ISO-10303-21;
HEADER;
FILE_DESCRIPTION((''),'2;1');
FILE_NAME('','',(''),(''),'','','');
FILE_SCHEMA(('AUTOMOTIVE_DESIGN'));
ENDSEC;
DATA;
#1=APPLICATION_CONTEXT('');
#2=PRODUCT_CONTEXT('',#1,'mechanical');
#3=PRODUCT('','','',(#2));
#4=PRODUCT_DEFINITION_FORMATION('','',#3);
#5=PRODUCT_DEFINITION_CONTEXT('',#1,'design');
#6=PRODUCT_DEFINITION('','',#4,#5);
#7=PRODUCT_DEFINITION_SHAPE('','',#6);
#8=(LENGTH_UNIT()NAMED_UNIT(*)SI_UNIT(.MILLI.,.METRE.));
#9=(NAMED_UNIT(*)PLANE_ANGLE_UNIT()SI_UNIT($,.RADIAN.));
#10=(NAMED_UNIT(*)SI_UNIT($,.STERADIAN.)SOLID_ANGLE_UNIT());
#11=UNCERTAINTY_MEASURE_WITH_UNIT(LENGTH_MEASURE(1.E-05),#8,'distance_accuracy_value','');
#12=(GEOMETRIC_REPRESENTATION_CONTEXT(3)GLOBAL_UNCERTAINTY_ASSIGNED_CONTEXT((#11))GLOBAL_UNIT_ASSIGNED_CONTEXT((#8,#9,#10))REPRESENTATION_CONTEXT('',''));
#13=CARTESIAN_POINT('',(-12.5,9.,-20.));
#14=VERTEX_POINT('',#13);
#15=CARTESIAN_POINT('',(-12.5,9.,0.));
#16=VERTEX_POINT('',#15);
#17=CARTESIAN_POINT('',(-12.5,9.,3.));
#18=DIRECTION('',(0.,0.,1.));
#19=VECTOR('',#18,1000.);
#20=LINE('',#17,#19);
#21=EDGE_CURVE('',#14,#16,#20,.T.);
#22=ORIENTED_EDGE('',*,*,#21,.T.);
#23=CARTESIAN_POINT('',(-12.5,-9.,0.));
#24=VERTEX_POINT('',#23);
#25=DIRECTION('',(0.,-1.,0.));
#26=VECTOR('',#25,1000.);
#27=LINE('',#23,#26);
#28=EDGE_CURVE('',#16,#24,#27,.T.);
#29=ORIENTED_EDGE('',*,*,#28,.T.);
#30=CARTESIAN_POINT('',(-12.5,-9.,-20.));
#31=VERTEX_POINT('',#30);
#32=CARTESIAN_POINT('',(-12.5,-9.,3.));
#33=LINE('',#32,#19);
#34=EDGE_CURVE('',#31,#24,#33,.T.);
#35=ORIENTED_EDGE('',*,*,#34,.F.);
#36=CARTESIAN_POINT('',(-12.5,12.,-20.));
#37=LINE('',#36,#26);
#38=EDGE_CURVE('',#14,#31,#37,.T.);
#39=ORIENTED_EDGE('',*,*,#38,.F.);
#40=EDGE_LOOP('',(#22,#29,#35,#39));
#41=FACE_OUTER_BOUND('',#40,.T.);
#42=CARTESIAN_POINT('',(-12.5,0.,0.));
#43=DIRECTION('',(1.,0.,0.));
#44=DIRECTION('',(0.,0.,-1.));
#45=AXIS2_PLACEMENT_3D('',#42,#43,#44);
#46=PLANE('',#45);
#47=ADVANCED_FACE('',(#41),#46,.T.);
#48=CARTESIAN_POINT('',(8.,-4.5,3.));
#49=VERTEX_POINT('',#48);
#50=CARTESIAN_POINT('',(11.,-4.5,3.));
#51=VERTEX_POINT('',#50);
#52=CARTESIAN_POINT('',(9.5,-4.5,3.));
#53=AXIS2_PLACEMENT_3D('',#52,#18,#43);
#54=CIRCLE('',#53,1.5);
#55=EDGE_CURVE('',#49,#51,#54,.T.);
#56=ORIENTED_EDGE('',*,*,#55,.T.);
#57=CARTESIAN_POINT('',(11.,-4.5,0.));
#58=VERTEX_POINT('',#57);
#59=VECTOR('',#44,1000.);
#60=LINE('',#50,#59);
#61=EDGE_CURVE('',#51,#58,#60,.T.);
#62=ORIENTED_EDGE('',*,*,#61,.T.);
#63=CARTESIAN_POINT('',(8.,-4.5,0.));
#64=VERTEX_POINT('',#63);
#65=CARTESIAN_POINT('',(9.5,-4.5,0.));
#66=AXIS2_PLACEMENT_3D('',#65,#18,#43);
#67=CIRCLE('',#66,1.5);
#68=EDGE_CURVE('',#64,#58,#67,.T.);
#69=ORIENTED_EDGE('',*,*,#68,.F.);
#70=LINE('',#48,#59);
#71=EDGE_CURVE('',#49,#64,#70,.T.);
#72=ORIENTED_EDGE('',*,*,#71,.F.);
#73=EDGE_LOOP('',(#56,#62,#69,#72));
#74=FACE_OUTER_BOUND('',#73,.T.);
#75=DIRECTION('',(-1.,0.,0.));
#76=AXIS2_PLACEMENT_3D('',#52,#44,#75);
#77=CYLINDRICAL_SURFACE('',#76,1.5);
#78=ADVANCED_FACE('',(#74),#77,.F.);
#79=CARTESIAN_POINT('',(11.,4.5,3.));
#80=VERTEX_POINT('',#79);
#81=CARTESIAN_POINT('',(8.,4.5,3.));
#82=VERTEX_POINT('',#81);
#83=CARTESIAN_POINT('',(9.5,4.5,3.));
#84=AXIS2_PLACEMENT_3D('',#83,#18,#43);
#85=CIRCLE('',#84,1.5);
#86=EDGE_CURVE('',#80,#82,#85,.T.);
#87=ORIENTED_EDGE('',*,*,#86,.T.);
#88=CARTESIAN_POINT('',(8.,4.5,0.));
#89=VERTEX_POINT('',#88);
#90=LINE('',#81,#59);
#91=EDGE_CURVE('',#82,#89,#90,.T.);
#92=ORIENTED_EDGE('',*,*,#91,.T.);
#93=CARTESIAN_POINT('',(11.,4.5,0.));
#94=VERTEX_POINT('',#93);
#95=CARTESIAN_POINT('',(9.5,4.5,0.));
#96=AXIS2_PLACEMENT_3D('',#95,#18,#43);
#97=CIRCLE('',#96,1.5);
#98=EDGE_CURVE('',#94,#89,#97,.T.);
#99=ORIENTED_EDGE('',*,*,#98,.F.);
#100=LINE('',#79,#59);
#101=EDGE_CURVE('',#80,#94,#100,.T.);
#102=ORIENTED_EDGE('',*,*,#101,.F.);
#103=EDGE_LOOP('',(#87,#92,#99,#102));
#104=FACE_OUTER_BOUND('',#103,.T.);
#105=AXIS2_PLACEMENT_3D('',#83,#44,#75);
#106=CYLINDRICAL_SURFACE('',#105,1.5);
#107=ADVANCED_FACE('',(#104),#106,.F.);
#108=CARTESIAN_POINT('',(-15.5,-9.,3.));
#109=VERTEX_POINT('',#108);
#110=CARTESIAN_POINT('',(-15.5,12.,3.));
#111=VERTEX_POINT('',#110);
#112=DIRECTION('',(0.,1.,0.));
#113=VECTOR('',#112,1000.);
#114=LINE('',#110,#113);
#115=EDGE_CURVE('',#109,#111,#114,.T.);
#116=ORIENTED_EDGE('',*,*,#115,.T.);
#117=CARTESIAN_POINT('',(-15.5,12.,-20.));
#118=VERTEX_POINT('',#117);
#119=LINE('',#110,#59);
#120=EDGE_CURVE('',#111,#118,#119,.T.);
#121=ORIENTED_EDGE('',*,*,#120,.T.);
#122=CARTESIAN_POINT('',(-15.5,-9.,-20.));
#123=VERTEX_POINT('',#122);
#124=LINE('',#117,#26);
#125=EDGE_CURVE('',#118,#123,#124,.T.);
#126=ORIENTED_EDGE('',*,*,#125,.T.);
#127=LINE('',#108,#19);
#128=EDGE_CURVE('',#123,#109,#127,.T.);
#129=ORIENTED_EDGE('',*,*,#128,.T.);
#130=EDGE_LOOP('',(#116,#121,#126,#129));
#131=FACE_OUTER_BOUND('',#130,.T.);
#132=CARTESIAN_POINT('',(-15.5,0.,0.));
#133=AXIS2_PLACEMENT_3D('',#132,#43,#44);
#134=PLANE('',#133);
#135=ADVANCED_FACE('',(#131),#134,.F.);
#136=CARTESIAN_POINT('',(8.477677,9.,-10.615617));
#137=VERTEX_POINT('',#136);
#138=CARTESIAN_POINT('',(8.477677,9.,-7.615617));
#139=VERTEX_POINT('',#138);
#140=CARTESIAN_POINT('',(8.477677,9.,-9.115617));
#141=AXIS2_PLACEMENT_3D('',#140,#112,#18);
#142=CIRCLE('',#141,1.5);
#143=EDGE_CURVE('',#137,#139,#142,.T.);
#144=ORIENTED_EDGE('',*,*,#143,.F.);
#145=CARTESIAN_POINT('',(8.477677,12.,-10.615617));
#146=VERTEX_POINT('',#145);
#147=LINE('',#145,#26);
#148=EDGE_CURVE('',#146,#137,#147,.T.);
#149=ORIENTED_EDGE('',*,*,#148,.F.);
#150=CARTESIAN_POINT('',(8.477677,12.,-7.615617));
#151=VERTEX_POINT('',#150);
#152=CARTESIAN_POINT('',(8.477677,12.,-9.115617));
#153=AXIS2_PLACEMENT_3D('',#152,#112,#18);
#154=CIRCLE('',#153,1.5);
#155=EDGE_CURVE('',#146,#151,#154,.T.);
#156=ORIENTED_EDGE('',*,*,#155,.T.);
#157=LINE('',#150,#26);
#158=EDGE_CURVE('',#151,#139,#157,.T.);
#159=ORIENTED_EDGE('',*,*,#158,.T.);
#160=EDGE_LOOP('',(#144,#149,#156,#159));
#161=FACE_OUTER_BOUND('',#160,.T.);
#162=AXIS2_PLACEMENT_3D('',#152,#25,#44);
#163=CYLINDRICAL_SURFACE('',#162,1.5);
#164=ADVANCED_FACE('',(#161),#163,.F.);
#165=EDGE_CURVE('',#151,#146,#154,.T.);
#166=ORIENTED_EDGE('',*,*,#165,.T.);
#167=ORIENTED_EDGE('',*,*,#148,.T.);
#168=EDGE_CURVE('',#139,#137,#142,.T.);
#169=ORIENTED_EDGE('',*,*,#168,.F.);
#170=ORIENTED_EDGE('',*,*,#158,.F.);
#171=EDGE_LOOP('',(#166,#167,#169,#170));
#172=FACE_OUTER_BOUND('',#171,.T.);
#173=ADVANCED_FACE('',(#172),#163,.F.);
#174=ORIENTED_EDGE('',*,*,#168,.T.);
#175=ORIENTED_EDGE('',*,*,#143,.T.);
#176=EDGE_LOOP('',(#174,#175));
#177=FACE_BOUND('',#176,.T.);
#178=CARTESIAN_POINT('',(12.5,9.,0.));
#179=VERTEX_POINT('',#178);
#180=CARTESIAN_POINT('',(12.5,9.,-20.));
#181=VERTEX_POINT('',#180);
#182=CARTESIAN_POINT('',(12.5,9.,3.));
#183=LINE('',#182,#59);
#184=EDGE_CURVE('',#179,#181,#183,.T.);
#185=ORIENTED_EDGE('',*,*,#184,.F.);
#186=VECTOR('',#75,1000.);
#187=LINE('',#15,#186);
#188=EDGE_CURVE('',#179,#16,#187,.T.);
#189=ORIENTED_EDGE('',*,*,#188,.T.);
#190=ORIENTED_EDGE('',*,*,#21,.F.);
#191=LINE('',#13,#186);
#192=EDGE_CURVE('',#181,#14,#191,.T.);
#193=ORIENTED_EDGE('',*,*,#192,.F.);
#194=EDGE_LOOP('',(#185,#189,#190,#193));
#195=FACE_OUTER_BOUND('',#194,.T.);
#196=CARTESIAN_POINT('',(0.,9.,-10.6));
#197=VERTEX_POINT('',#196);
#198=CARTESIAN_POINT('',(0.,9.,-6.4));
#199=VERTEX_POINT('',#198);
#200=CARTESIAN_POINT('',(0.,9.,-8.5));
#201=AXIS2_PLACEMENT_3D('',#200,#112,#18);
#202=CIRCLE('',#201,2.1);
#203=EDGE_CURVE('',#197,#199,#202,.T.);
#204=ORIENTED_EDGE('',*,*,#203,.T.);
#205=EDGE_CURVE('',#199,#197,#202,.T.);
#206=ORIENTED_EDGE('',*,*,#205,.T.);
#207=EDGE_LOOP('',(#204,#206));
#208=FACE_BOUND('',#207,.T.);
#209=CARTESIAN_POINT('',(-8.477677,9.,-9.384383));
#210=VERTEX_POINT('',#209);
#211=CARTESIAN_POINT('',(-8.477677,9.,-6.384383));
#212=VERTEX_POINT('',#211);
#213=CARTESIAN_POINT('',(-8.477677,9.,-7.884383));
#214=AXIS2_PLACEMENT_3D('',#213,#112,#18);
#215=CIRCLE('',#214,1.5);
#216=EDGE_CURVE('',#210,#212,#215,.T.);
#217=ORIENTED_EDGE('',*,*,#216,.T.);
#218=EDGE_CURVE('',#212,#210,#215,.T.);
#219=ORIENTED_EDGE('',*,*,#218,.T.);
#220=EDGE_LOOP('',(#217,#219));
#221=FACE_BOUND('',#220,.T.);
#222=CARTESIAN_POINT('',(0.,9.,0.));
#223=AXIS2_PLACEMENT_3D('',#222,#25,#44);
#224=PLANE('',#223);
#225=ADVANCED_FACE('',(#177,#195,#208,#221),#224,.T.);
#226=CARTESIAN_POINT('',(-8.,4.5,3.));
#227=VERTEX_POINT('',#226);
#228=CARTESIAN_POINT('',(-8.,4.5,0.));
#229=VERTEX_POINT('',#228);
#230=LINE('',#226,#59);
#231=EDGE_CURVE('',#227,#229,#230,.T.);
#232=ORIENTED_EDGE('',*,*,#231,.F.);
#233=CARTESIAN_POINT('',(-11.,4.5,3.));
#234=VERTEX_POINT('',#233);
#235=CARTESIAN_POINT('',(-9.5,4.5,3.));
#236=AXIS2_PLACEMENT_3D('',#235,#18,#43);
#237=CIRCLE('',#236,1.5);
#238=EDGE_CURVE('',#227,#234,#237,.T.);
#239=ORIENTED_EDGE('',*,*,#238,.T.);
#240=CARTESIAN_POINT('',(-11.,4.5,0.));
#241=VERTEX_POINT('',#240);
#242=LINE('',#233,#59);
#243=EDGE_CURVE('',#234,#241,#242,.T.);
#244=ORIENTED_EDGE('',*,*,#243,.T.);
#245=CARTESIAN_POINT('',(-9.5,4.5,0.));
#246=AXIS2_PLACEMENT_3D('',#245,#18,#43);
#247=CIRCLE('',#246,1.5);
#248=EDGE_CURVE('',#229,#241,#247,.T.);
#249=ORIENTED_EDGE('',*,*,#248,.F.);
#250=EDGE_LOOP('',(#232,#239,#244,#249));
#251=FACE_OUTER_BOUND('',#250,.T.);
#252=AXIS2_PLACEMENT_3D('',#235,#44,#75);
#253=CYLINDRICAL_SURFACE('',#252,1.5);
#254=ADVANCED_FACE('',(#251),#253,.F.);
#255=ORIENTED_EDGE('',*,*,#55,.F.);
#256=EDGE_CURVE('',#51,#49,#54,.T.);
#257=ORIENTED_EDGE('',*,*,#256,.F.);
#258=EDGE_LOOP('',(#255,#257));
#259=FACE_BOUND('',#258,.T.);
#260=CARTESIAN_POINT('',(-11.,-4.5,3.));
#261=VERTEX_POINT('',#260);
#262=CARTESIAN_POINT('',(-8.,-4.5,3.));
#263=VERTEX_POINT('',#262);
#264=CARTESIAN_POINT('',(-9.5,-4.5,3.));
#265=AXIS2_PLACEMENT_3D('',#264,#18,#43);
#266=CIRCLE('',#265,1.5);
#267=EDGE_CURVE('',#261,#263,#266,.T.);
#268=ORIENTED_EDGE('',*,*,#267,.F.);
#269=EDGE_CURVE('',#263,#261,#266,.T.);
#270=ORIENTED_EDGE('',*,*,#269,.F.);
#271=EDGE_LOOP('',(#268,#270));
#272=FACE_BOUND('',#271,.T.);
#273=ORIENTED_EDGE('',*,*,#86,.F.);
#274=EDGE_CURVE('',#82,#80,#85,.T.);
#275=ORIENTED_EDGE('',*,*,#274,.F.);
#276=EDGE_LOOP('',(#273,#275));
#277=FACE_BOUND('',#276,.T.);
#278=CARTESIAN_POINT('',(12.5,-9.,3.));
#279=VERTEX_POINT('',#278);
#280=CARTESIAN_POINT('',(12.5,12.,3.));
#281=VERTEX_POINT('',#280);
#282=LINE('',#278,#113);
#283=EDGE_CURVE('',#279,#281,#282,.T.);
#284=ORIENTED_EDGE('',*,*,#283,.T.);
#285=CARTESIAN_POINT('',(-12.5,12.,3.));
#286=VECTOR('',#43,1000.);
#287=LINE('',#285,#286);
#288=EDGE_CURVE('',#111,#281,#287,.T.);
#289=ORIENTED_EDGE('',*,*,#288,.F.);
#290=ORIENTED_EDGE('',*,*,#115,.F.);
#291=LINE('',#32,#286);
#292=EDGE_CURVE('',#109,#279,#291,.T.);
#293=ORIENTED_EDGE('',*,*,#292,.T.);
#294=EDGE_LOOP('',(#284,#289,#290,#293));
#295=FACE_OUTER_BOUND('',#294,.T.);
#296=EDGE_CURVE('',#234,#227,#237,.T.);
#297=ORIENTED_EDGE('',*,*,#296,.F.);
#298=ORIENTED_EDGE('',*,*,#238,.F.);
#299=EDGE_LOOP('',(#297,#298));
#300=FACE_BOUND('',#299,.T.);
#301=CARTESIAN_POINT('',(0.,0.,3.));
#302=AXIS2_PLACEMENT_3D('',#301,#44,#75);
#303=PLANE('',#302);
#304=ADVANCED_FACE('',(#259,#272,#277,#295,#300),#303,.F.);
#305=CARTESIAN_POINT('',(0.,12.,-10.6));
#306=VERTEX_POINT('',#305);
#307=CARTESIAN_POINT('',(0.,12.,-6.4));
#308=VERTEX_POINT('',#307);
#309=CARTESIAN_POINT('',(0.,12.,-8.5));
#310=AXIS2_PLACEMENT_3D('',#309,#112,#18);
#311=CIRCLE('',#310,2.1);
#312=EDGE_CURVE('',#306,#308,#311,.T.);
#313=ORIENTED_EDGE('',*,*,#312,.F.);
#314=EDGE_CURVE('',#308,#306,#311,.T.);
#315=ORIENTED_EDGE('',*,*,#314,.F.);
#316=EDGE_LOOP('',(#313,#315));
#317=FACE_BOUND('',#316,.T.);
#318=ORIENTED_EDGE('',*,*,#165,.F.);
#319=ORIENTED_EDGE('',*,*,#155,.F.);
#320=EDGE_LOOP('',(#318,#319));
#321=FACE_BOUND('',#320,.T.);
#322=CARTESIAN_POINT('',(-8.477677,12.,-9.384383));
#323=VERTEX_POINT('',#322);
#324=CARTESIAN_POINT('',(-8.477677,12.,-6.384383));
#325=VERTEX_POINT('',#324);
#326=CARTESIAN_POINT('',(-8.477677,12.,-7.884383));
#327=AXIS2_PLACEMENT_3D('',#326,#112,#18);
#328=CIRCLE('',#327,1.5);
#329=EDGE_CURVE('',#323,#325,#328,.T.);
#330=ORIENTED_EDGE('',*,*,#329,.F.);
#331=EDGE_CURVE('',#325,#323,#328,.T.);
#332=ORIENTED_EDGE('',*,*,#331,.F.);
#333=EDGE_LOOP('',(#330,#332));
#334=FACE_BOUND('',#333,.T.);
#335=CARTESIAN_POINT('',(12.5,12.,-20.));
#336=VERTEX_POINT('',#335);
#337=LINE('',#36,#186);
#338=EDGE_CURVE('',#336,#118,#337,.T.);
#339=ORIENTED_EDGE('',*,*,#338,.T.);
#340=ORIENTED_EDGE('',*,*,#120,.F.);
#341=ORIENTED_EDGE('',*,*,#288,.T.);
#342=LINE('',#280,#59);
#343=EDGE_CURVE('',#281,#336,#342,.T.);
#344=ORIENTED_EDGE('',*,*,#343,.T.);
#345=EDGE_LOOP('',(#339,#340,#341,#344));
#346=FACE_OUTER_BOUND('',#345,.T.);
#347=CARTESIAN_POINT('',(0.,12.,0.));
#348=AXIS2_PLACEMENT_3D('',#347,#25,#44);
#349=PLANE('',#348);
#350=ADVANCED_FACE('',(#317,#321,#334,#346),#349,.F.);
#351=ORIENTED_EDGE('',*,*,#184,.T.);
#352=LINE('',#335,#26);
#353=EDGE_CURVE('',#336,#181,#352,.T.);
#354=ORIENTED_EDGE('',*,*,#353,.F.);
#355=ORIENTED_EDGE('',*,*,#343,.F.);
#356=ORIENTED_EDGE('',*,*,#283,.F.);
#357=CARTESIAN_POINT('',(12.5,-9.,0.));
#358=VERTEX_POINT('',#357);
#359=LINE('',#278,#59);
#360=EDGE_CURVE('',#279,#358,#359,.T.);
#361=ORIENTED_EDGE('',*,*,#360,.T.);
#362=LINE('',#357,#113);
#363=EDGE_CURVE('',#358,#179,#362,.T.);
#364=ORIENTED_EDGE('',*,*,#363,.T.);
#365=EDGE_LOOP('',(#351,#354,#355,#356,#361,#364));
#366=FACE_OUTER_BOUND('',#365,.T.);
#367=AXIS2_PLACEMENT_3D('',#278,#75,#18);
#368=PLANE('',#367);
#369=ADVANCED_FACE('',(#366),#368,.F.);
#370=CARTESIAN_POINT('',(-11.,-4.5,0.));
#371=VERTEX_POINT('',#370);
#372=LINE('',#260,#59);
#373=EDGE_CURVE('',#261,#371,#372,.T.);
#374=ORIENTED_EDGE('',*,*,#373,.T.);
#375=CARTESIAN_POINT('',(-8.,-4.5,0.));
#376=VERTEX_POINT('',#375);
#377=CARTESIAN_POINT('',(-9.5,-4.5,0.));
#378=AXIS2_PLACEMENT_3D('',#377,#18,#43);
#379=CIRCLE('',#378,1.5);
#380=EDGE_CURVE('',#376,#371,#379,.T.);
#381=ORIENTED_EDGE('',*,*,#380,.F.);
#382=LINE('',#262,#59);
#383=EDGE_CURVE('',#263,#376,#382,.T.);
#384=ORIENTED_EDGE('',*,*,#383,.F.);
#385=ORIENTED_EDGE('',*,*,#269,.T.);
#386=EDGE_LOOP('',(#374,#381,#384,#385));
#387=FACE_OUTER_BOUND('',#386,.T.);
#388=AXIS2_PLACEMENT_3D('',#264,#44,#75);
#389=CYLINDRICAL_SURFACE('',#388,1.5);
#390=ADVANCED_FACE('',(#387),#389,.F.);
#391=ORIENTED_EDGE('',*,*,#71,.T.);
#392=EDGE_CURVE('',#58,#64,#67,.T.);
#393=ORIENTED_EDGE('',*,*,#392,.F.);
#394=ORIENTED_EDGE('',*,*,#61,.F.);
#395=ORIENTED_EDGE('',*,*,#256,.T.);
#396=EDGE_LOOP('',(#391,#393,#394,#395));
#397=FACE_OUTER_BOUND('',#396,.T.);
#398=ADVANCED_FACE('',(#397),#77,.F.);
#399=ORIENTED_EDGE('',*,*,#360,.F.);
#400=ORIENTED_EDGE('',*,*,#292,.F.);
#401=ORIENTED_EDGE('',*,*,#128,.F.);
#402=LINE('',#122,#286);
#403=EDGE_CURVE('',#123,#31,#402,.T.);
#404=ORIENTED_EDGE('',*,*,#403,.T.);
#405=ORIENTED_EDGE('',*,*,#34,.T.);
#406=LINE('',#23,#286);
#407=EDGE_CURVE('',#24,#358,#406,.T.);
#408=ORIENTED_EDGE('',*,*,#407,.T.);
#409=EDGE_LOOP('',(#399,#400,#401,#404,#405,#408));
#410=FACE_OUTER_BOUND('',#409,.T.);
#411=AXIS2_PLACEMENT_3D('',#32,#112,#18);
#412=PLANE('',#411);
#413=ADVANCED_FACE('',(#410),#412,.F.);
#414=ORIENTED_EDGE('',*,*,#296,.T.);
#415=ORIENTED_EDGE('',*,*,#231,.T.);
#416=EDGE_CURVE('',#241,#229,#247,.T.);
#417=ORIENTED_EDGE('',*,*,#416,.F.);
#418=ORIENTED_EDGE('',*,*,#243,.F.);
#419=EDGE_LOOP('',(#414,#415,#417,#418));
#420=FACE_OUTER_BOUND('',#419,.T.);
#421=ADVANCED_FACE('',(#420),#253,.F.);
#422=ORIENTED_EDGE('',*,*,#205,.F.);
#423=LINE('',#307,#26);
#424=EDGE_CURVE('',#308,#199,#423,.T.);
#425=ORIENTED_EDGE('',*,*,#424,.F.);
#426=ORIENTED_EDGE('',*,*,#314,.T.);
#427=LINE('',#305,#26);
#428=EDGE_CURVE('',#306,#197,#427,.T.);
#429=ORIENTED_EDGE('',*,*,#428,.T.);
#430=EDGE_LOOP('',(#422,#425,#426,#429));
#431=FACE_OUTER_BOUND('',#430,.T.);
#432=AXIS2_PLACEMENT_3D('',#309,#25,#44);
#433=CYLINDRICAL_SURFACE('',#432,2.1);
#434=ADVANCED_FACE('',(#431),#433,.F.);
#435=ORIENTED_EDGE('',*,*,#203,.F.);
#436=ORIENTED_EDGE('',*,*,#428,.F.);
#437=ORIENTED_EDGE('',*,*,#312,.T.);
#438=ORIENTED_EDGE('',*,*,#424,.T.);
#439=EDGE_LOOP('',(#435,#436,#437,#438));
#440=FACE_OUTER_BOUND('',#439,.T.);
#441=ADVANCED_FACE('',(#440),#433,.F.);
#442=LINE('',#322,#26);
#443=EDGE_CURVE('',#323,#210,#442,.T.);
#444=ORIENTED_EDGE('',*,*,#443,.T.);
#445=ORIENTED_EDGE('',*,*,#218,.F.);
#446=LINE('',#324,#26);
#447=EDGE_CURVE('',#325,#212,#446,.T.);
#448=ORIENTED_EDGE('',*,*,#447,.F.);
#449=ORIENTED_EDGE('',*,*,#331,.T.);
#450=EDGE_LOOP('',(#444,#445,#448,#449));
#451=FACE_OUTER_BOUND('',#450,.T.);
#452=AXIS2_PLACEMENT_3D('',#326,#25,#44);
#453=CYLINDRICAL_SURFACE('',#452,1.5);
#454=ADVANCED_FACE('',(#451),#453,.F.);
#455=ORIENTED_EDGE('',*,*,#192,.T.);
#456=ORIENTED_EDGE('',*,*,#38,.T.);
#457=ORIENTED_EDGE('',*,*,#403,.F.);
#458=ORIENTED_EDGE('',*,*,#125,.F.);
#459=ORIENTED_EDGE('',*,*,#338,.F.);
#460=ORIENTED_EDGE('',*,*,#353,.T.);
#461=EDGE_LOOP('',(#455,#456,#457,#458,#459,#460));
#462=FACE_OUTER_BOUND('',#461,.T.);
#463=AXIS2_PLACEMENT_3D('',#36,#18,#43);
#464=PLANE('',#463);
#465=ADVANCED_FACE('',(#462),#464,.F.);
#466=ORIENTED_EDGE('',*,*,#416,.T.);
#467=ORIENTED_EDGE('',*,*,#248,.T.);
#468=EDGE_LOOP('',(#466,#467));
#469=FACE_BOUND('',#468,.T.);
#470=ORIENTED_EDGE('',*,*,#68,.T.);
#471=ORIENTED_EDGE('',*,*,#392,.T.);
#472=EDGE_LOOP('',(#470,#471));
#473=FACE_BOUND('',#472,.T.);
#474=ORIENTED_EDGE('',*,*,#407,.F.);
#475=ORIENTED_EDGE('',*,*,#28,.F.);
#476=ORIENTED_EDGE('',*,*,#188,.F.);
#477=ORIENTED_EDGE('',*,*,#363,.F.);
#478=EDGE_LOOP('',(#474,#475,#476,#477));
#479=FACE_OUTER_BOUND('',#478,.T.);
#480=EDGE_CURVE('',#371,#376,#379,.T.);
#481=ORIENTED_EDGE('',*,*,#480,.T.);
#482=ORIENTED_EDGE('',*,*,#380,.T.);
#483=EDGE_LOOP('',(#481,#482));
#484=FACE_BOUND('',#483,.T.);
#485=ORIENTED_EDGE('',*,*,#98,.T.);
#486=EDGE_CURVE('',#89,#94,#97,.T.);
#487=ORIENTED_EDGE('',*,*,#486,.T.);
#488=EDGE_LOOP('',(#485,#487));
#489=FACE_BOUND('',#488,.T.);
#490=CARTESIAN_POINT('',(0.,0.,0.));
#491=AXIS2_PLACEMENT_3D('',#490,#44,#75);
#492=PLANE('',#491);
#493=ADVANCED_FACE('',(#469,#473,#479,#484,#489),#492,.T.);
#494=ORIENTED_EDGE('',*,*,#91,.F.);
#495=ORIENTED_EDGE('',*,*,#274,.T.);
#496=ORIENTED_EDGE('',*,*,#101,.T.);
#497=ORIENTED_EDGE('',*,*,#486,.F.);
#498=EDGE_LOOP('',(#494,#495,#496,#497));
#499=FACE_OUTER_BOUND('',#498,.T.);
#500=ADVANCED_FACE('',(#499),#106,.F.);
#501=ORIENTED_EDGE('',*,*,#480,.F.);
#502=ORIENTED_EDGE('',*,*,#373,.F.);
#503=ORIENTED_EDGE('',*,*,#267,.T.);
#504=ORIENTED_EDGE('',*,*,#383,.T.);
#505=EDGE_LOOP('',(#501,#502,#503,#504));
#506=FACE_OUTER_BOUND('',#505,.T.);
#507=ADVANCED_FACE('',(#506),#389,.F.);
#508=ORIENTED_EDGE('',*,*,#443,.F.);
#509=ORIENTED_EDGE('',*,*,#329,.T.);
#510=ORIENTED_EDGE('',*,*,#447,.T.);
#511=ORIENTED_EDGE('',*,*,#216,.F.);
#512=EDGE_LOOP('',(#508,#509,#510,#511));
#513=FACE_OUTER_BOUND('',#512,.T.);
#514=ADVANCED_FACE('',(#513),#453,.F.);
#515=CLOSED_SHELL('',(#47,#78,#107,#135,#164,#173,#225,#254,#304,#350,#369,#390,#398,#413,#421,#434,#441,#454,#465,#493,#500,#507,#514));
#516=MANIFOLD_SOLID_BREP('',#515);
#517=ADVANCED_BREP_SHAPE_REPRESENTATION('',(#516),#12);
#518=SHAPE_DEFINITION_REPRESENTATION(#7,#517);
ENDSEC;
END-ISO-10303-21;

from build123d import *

# Parameters (mm, degrees)
SKETCH1_W           = 25
SKETCH1_H           = 18
SKETCH1_R           = 1.5
BOSS_EXTRUDE1_DEPTH = 3
SKETCH2_W           = 25
SKETCH2_H           = 23
SKETCH2_R           = 2.1
SKETCH2_R_2         = 1.5
BOSS_EXTRUDE2_DEPTH = 3
SKETCH3_W           = 23
SKETCH3_H           = 21
BOSS_EXTRUDE3_DEPTH = 3


with BuildPart() as part:
    # Sketch1 → Boss-Extrude1 (new body)
    with BuildSketch(Plane.XY):
        Rectangle(SKETCH1_W, SKETCH1_H)
        with Locations((-9.5, 4.5)):
            Circle(SKETCH1_R, mode=Mode.SUBTRACT)
        with Locations((9.5, 4.5)):
            Circle(SKETCH1_R, mode=Mode.SUBTRACT)
        with Locations((9.5, -4.5)):
            Circle(SKETCH1_R, mode=Mode.SUBTRACT)
        with Locations((-9.5, -4.5)):
            Circle(SKETCH1_R, mode=Mode.SUBTRACT)
    extrude(amount=BOSS_EXTRUDE1_DEPTH)

    # Sketch2 → Boss-Extrude2 (add)
    with BuildSketch(Plane(origin=(0, 9, 0), x_dir=(1, 0, 0), z_dir=(0, 1, 0))):
        with Locations((0, 8.5)):
            Rectangle(SKETCH2_W, SKETCH2_H)
        with Locations(Location((0, 8.5, 0), (0, 0, 270))):
            Circle(SKETCH2_R, mode=Mode.SUBTRACT)
        with Locations(Location((-8.477677472, 7.884382628, 0), (0, 0, 270))):
            Circle(SKETCH2_R_2, mode=Mode.SUBTRACT)
        with Locations(Location((8.477677464, 9.115617375, 0), (0, 0, 270))):
            Circle(SKETCH2_R_2, mode=Mode.SUBTRACT)
    extrude(amount=BOSS_EXTRUDE2_DEPTH)

    # Sketch3 → Boss-Extrude3 (add)
    with BuildSketch(Plane.ZY.offset(12.5)):
        with Locations((-8.5, 1.5)):
            Rectangle(SKETCH3_W, SKETCH3_H)
    extrude(amount=BOSS_EXTRUDE3_DEPTH)


solid = part.part
